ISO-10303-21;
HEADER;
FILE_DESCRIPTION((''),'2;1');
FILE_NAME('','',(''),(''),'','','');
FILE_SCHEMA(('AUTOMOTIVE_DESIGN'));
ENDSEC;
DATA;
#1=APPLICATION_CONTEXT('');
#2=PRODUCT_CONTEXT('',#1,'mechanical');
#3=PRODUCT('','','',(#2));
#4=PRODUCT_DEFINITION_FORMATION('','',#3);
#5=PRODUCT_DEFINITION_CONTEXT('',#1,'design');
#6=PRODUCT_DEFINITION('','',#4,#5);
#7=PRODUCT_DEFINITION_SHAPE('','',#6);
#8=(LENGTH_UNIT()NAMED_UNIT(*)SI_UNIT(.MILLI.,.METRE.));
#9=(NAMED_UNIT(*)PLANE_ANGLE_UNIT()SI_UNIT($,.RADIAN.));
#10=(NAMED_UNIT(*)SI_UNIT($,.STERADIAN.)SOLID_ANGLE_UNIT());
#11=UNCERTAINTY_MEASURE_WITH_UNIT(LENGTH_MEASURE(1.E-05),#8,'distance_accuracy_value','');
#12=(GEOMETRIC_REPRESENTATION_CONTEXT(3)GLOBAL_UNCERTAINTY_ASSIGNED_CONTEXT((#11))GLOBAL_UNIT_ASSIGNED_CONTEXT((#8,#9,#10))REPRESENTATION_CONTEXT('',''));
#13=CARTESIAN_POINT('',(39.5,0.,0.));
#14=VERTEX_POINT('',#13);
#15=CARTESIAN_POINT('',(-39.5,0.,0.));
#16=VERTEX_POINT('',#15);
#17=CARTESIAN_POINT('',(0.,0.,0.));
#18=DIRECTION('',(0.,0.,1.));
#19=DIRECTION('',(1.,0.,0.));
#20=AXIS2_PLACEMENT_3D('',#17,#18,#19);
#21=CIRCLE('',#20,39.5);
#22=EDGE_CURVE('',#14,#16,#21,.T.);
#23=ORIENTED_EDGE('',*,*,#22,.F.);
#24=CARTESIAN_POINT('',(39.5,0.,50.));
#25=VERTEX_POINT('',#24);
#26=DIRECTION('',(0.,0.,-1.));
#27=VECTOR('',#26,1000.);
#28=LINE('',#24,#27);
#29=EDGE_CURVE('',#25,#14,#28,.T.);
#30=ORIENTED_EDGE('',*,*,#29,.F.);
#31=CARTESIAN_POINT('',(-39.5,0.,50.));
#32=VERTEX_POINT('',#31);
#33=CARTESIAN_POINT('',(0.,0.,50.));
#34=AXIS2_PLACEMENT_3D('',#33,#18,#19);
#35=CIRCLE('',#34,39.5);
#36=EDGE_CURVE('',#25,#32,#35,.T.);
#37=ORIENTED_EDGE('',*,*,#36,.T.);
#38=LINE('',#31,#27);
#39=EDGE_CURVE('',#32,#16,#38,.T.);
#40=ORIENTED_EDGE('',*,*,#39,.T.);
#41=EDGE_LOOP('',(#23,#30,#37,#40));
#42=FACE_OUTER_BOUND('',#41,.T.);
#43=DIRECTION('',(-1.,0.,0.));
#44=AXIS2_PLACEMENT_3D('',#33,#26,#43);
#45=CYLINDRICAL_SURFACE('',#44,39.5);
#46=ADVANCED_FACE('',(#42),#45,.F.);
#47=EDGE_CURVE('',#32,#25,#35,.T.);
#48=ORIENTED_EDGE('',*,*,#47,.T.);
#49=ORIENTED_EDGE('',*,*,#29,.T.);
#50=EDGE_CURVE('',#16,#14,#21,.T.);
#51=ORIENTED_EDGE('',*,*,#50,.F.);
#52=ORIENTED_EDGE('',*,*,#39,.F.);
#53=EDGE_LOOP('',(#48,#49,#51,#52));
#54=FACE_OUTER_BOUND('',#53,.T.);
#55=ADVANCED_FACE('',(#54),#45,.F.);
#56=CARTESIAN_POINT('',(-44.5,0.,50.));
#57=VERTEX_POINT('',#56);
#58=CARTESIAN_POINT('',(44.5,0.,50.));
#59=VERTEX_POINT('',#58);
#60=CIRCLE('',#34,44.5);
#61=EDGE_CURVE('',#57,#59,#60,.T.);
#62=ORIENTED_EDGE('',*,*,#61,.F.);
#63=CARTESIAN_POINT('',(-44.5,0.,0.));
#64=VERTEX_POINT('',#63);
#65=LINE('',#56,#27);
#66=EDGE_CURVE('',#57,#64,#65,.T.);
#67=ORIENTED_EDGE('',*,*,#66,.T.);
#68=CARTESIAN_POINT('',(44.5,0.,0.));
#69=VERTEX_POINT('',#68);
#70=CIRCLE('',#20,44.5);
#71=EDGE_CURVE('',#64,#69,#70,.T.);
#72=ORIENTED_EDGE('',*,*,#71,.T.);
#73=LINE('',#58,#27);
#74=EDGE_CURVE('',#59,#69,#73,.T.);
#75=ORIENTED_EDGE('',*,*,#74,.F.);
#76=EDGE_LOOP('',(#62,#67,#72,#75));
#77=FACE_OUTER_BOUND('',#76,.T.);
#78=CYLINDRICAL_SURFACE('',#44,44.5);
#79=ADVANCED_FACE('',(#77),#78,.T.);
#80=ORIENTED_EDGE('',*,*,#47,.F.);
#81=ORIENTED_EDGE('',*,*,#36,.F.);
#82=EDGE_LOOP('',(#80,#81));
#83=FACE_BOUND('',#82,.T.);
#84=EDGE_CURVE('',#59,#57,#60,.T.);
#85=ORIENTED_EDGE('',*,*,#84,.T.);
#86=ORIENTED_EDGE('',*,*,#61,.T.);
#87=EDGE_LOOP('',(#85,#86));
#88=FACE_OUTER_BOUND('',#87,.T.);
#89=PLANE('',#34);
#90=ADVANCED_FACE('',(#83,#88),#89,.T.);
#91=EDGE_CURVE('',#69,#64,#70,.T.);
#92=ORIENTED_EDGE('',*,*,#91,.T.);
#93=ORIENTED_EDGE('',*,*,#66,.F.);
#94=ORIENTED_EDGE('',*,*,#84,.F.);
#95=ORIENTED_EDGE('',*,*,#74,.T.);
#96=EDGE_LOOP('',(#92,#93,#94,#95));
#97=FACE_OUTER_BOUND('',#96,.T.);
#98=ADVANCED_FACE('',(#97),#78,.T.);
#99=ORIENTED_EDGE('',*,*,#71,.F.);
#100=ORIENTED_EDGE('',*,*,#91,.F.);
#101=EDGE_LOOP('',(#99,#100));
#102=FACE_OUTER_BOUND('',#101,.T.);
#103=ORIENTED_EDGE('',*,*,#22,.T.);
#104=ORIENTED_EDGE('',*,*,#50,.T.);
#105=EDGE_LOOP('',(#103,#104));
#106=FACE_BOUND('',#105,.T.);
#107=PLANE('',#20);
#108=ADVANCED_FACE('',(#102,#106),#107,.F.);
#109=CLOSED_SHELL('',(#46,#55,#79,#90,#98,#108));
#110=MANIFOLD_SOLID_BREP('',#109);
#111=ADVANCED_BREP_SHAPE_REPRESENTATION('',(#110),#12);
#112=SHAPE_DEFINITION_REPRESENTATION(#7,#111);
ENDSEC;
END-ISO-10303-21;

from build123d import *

# Parameters (mm, degrees)
SKETCH1_R           = 44.5
SKETCH1_R_2         = 39.5
BOSS_EXTRUDE1_DEPTH = 50


with BuildPart() as part:
    # Sketch1 → Boss-Extrude1 (new body)
    with BuildSketch(Plane.XY):
        Circle(SKETCH1_R)
        Circle(SKETCH1_R_2, mode=Mode.SUBTRACT)
    extrude(amount=BOSS_EXTRUDE1_DEPTH)


solid = part.part
